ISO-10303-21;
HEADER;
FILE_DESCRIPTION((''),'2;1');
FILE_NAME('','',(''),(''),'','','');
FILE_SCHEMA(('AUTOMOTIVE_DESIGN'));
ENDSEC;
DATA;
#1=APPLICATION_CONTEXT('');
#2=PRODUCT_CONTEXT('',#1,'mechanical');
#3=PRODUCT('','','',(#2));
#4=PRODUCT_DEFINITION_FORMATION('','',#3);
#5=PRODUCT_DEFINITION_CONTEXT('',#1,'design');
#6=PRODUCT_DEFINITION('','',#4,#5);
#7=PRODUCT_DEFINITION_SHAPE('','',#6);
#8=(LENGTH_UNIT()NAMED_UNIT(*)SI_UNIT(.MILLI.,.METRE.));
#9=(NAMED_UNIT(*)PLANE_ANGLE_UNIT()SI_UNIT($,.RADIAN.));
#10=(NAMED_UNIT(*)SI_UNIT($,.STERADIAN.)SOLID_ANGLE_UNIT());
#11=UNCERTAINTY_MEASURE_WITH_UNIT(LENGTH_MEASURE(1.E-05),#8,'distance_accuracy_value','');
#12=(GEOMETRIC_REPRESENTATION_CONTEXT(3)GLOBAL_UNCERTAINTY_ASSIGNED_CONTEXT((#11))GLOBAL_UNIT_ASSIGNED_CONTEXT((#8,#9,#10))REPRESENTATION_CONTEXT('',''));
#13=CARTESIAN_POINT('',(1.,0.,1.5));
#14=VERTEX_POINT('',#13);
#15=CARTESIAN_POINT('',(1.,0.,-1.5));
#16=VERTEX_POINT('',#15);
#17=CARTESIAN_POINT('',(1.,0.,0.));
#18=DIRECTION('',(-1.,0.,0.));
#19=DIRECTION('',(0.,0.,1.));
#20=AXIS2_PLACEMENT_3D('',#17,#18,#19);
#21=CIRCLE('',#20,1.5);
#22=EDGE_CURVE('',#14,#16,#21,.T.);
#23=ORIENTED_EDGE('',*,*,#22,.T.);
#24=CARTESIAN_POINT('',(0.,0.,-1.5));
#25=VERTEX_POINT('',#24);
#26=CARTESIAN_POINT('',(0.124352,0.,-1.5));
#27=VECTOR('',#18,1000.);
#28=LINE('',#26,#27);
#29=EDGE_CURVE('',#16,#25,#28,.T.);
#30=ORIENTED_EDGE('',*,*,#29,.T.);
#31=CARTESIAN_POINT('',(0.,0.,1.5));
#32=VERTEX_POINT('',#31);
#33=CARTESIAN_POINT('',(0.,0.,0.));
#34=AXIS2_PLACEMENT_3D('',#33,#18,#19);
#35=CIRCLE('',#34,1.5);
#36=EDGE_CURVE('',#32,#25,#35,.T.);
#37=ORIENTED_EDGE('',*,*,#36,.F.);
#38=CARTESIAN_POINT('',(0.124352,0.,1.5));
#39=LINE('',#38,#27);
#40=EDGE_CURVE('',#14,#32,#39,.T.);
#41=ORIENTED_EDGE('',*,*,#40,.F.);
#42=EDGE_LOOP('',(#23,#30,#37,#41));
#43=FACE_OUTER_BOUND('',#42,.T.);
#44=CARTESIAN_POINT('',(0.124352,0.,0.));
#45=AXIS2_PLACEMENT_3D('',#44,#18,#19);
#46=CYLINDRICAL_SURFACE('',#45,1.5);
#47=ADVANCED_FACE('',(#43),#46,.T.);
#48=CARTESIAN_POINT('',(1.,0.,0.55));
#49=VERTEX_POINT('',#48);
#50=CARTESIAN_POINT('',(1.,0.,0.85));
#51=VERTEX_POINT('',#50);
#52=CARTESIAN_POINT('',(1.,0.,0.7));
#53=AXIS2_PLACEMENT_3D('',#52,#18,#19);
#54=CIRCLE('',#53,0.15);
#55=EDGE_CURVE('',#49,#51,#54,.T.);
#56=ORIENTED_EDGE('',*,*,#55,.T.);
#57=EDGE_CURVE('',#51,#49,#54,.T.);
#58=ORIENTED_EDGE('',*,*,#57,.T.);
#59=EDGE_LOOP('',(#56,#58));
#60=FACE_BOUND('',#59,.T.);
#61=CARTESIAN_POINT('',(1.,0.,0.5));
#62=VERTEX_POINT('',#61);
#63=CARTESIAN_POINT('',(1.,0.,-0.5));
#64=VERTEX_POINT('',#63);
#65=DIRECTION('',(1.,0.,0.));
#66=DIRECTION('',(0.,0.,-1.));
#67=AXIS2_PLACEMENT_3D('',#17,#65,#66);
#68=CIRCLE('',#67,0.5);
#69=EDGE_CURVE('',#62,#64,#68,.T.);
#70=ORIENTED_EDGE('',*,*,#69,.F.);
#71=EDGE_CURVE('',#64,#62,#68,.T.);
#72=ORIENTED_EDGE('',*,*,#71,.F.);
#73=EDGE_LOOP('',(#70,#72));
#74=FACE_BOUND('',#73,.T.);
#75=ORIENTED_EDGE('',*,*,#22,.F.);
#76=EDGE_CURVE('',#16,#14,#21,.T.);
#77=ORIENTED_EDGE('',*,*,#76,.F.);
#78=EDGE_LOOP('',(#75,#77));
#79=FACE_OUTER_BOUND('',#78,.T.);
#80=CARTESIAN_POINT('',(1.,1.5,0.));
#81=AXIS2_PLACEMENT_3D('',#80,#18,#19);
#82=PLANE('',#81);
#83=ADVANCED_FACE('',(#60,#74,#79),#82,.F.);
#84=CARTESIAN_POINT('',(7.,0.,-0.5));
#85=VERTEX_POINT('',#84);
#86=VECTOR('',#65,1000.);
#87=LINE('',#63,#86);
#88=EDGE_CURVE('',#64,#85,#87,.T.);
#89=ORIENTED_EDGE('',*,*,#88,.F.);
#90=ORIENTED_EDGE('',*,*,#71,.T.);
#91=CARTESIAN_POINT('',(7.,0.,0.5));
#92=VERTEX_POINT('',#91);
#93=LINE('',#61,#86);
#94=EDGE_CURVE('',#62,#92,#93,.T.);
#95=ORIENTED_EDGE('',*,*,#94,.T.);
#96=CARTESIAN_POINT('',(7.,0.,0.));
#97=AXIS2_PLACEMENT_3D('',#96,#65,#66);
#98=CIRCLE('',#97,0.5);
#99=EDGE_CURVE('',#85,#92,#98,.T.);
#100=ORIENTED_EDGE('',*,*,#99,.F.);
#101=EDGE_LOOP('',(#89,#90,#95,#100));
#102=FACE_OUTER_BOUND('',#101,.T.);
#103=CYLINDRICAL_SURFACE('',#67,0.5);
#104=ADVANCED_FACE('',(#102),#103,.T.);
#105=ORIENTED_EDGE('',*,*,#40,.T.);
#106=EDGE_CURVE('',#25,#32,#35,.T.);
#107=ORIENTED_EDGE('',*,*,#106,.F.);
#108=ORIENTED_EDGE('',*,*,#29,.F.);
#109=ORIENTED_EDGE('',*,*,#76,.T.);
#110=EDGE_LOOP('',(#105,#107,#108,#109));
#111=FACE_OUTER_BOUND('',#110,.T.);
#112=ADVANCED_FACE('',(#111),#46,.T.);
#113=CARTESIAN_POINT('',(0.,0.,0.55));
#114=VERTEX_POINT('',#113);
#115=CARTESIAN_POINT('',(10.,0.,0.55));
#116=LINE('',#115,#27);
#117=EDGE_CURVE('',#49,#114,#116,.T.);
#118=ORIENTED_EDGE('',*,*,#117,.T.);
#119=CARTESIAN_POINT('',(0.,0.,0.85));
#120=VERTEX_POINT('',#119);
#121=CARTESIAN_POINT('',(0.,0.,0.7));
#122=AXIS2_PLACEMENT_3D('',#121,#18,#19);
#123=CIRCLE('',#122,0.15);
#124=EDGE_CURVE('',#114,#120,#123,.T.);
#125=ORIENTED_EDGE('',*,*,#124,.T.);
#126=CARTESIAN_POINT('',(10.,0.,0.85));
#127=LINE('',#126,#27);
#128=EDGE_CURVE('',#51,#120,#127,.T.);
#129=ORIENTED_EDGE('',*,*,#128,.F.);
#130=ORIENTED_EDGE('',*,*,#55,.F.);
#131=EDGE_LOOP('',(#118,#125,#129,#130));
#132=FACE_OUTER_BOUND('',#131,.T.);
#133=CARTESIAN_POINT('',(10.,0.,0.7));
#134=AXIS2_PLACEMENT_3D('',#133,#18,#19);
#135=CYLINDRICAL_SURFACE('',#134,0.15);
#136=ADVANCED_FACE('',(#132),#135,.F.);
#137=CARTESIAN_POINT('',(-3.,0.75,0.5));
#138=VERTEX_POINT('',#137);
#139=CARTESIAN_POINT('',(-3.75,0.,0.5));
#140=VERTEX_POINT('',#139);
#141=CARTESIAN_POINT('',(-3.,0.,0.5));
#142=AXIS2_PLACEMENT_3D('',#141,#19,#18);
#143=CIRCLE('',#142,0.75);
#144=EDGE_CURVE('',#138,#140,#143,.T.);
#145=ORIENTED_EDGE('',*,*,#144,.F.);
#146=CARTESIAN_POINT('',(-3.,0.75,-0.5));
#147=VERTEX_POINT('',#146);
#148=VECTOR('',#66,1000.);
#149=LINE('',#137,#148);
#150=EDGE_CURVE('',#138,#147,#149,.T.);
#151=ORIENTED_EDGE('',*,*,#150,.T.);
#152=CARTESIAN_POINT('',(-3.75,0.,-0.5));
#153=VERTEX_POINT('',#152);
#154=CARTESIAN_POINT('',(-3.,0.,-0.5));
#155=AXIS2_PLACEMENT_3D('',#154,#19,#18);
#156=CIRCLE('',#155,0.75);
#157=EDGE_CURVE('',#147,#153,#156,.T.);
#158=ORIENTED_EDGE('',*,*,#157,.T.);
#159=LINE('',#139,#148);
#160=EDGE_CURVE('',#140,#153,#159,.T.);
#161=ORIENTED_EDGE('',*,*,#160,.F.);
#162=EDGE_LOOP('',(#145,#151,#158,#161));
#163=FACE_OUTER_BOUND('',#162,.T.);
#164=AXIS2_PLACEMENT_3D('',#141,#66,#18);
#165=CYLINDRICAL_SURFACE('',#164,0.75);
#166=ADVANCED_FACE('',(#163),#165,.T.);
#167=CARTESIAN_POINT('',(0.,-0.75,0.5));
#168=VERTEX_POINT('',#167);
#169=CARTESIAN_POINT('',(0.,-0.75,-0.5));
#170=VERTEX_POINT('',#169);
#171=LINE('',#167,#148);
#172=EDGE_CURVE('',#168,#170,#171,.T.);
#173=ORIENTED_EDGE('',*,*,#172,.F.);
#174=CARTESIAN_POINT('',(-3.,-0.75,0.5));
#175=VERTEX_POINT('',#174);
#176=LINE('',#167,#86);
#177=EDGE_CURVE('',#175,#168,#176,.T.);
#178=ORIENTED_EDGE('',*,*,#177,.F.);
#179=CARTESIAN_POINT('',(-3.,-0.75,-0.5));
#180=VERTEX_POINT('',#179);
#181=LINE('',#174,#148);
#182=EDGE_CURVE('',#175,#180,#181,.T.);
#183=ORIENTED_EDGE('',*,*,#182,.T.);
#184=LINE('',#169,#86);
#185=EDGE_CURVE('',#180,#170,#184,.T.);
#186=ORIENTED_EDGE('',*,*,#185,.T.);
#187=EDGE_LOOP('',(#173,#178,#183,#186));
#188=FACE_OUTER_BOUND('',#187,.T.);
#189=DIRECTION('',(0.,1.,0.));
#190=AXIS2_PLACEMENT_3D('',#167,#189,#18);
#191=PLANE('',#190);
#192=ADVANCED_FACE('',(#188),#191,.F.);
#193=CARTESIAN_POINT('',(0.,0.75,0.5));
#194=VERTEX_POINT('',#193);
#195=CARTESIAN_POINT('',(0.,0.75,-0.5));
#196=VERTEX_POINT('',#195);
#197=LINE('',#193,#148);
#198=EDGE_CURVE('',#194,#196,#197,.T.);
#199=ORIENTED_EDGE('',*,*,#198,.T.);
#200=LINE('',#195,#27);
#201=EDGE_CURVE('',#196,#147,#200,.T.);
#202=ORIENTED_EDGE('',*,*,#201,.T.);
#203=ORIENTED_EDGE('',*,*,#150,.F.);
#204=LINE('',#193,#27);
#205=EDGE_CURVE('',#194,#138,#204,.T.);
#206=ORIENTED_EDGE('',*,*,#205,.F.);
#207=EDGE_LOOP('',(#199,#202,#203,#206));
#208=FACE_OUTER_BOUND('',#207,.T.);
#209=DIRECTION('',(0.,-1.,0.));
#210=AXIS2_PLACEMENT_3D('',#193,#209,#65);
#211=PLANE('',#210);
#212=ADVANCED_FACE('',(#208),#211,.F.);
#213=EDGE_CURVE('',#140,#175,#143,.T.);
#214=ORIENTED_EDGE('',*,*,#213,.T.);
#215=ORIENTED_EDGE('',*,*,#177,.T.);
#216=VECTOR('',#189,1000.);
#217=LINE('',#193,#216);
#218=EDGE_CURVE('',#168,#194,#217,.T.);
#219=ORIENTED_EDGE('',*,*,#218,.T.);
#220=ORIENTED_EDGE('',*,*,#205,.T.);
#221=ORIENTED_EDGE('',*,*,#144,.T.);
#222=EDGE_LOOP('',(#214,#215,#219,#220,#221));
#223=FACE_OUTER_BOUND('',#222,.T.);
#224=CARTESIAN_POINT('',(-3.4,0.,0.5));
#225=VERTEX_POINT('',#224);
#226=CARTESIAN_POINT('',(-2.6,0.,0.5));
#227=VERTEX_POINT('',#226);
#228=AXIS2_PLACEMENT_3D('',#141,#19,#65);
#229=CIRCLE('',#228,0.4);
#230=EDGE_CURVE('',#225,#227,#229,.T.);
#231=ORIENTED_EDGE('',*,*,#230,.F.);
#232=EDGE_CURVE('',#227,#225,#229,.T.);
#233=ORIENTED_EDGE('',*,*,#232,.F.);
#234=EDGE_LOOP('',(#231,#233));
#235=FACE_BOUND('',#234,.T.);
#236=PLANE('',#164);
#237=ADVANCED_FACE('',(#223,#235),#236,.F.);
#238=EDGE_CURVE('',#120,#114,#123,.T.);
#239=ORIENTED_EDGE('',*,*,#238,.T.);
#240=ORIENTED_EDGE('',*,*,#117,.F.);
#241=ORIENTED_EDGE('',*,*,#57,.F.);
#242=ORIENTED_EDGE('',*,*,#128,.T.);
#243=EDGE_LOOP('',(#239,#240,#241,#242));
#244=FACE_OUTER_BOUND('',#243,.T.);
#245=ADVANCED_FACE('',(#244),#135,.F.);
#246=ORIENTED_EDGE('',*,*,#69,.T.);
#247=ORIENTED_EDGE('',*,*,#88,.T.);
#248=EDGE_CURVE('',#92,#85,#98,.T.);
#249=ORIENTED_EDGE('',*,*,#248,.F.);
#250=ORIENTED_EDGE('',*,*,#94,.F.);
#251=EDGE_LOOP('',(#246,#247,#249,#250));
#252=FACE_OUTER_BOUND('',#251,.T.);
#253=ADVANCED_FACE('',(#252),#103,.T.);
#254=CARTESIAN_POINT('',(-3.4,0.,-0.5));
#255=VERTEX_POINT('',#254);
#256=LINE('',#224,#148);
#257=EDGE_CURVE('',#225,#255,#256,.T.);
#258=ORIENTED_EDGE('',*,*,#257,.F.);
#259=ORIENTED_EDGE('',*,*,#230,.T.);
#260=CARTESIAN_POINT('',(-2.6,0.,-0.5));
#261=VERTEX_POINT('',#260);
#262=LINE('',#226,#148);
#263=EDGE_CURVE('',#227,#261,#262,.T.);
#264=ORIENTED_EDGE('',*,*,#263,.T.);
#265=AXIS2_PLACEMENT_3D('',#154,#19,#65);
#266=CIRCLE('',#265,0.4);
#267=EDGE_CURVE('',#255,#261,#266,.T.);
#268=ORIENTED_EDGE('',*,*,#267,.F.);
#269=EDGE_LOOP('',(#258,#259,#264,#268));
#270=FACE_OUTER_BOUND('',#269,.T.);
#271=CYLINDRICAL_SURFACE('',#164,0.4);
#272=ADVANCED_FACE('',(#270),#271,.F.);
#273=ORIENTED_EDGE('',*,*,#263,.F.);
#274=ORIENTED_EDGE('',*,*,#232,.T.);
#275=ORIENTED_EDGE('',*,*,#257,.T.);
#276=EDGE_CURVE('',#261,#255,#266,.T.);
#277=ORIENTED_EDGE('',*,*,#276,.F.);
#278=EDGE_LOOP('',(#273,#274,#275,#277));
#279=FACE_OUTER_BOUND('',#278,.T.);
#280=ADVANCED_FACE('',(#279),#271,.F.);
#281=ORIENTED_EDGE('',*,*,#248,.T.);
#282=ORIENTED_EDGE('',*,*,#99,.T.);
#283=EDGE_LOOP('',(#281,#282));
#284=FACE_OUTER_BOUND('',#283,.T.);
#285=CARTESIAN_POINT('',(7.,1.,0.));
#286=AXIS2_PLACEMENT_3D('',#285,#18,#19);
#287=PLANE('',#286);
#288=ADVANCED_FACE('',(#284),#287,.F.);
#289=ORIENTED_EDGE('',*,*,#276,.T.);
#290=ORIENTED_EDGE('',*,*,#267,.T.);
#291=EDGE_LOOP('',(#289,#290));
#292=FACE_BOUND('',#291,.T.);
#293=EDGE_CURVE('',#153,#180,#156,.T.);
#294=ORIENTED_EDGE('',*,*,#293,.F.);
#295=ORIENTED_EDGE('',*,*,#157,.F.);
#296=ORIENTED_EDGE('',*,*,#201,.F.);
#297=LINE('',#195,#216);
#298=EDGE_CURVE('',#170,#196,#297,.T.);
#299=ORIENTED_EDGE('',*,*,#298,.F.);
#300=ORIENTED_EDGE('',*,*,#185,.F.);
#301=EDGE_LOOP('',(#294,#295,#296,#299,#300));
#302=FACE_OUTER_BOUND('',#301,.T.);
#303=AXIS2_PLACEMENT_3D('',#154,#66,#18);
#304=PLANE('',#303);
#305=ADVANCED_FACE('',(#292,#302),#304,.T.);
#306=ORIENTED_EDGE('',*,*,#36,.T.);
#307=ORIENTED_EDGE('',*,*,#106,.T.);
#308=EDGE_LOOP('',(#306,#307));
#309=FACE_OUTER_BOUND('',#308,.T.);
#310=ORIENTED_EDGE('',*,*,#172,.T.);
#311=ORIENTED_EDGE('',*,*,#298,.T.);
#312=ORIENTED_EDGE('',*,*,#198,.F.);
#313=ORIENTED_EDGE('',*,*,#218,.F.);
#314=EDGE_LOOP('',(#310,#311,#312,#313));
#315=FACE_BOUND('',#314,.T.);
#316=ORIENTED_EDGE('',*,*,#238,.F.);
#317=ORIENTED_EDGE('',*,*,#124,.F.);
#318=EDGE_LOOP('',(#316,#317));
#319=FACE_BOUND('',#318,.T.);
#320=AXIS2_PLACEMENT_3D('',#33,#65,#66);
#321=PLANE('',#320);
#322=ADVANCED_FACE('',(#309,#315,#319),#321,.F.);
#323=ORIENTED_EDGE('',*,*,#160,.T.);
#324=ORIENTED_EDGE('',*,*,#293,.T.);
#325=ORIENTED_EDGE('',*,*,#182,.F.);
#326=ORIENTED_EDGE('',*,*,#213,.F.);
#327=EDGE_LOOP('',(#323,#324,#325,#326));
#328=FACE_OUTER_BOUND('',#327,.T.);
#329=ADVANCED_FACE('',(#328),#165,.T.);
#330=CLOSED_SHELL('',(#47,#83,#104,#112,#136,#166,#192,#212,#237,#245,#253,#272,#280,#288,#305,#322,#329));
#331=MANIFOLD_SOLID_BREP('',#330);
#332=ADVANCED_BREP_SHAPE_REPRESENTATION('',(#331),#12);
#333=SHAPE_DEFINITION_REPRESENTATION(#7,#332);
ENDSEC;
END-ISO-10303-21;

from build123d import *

# Parameters (mm, degrees)
SKETCH2_R           = 0.4
BOSS_EXTRUDE1_DEPTH = 0.5
SKETCH4_R           = 1
SKETCH4_R_2         = 0.5
CUT_EXTRUDE3_DEPTH  = 6
SKETCH5_R           = 0.15
CUT_EXTRUDE4_DEPTH  = 10


with BuildPart() as part:
    # Sketch1 → Revolve1 (revolve)
    with BuildSketch(Plane.XY, mode=Mode.PRIVATE) as revolve1_sk:
        Polygon((0, 0), (0, 1.5), (1, 1.5), (1, 1), (7, 1), (7, 0), align=None)
    revolve(revolve1_sk.sketch.rotate(Axis((0.124352332, 0, 0), (1, 0, 0)), 90), axis=Axis((0.124352332, 0, 0), (1, 0, 0)))

    # Sketch2 → Boss-Extrude1 (add, symmetric)
    with BuildSketch(Plane.XY):
        with BuildLine():
            Line((0, 0.75), (0, -0.75))
            Line((0, -0.75), (-3, -0.75))
            ThreePointArc((-3, -0.75), (-3.75, 0), (-3, 0.75))
            Line((-3, 0.75), (0, 0.75))
        make_face()
        with Locations((-3, 0)):
            Circle(SKETCH2_R, mode=Mode.SUBTRACT)
    extrude(amount=BOSS_EXTRUDE1_DEPTH, both=True)

    # Sketch4 → Cut-Extrude3 (cut)
    with BuildSketch(Plane(origin=(7, 0, 0), x_dir=(0, 0, -1), z_dir=(1, 0, 0))):
        Circle(SKETCH4_R)
        Circle(SKETCH4_R_2, mode=Mode.SUBTRACT)
    extrude(amount=-CUT_EXTRUDE3_DEPTH, mode=Mode.SUBTRACT)

    # Sketch5 → Cut-Extrude4 (cut)
    with BuildSketch(Plane.ZY):
        with Locations((0.7, 0)):
            Circle(SKETCH5_R)
    extrude(amount=-CUT_EXTRUDE4_DEPTH, mode=Mode.SUBTRACT)


solid = part.part
